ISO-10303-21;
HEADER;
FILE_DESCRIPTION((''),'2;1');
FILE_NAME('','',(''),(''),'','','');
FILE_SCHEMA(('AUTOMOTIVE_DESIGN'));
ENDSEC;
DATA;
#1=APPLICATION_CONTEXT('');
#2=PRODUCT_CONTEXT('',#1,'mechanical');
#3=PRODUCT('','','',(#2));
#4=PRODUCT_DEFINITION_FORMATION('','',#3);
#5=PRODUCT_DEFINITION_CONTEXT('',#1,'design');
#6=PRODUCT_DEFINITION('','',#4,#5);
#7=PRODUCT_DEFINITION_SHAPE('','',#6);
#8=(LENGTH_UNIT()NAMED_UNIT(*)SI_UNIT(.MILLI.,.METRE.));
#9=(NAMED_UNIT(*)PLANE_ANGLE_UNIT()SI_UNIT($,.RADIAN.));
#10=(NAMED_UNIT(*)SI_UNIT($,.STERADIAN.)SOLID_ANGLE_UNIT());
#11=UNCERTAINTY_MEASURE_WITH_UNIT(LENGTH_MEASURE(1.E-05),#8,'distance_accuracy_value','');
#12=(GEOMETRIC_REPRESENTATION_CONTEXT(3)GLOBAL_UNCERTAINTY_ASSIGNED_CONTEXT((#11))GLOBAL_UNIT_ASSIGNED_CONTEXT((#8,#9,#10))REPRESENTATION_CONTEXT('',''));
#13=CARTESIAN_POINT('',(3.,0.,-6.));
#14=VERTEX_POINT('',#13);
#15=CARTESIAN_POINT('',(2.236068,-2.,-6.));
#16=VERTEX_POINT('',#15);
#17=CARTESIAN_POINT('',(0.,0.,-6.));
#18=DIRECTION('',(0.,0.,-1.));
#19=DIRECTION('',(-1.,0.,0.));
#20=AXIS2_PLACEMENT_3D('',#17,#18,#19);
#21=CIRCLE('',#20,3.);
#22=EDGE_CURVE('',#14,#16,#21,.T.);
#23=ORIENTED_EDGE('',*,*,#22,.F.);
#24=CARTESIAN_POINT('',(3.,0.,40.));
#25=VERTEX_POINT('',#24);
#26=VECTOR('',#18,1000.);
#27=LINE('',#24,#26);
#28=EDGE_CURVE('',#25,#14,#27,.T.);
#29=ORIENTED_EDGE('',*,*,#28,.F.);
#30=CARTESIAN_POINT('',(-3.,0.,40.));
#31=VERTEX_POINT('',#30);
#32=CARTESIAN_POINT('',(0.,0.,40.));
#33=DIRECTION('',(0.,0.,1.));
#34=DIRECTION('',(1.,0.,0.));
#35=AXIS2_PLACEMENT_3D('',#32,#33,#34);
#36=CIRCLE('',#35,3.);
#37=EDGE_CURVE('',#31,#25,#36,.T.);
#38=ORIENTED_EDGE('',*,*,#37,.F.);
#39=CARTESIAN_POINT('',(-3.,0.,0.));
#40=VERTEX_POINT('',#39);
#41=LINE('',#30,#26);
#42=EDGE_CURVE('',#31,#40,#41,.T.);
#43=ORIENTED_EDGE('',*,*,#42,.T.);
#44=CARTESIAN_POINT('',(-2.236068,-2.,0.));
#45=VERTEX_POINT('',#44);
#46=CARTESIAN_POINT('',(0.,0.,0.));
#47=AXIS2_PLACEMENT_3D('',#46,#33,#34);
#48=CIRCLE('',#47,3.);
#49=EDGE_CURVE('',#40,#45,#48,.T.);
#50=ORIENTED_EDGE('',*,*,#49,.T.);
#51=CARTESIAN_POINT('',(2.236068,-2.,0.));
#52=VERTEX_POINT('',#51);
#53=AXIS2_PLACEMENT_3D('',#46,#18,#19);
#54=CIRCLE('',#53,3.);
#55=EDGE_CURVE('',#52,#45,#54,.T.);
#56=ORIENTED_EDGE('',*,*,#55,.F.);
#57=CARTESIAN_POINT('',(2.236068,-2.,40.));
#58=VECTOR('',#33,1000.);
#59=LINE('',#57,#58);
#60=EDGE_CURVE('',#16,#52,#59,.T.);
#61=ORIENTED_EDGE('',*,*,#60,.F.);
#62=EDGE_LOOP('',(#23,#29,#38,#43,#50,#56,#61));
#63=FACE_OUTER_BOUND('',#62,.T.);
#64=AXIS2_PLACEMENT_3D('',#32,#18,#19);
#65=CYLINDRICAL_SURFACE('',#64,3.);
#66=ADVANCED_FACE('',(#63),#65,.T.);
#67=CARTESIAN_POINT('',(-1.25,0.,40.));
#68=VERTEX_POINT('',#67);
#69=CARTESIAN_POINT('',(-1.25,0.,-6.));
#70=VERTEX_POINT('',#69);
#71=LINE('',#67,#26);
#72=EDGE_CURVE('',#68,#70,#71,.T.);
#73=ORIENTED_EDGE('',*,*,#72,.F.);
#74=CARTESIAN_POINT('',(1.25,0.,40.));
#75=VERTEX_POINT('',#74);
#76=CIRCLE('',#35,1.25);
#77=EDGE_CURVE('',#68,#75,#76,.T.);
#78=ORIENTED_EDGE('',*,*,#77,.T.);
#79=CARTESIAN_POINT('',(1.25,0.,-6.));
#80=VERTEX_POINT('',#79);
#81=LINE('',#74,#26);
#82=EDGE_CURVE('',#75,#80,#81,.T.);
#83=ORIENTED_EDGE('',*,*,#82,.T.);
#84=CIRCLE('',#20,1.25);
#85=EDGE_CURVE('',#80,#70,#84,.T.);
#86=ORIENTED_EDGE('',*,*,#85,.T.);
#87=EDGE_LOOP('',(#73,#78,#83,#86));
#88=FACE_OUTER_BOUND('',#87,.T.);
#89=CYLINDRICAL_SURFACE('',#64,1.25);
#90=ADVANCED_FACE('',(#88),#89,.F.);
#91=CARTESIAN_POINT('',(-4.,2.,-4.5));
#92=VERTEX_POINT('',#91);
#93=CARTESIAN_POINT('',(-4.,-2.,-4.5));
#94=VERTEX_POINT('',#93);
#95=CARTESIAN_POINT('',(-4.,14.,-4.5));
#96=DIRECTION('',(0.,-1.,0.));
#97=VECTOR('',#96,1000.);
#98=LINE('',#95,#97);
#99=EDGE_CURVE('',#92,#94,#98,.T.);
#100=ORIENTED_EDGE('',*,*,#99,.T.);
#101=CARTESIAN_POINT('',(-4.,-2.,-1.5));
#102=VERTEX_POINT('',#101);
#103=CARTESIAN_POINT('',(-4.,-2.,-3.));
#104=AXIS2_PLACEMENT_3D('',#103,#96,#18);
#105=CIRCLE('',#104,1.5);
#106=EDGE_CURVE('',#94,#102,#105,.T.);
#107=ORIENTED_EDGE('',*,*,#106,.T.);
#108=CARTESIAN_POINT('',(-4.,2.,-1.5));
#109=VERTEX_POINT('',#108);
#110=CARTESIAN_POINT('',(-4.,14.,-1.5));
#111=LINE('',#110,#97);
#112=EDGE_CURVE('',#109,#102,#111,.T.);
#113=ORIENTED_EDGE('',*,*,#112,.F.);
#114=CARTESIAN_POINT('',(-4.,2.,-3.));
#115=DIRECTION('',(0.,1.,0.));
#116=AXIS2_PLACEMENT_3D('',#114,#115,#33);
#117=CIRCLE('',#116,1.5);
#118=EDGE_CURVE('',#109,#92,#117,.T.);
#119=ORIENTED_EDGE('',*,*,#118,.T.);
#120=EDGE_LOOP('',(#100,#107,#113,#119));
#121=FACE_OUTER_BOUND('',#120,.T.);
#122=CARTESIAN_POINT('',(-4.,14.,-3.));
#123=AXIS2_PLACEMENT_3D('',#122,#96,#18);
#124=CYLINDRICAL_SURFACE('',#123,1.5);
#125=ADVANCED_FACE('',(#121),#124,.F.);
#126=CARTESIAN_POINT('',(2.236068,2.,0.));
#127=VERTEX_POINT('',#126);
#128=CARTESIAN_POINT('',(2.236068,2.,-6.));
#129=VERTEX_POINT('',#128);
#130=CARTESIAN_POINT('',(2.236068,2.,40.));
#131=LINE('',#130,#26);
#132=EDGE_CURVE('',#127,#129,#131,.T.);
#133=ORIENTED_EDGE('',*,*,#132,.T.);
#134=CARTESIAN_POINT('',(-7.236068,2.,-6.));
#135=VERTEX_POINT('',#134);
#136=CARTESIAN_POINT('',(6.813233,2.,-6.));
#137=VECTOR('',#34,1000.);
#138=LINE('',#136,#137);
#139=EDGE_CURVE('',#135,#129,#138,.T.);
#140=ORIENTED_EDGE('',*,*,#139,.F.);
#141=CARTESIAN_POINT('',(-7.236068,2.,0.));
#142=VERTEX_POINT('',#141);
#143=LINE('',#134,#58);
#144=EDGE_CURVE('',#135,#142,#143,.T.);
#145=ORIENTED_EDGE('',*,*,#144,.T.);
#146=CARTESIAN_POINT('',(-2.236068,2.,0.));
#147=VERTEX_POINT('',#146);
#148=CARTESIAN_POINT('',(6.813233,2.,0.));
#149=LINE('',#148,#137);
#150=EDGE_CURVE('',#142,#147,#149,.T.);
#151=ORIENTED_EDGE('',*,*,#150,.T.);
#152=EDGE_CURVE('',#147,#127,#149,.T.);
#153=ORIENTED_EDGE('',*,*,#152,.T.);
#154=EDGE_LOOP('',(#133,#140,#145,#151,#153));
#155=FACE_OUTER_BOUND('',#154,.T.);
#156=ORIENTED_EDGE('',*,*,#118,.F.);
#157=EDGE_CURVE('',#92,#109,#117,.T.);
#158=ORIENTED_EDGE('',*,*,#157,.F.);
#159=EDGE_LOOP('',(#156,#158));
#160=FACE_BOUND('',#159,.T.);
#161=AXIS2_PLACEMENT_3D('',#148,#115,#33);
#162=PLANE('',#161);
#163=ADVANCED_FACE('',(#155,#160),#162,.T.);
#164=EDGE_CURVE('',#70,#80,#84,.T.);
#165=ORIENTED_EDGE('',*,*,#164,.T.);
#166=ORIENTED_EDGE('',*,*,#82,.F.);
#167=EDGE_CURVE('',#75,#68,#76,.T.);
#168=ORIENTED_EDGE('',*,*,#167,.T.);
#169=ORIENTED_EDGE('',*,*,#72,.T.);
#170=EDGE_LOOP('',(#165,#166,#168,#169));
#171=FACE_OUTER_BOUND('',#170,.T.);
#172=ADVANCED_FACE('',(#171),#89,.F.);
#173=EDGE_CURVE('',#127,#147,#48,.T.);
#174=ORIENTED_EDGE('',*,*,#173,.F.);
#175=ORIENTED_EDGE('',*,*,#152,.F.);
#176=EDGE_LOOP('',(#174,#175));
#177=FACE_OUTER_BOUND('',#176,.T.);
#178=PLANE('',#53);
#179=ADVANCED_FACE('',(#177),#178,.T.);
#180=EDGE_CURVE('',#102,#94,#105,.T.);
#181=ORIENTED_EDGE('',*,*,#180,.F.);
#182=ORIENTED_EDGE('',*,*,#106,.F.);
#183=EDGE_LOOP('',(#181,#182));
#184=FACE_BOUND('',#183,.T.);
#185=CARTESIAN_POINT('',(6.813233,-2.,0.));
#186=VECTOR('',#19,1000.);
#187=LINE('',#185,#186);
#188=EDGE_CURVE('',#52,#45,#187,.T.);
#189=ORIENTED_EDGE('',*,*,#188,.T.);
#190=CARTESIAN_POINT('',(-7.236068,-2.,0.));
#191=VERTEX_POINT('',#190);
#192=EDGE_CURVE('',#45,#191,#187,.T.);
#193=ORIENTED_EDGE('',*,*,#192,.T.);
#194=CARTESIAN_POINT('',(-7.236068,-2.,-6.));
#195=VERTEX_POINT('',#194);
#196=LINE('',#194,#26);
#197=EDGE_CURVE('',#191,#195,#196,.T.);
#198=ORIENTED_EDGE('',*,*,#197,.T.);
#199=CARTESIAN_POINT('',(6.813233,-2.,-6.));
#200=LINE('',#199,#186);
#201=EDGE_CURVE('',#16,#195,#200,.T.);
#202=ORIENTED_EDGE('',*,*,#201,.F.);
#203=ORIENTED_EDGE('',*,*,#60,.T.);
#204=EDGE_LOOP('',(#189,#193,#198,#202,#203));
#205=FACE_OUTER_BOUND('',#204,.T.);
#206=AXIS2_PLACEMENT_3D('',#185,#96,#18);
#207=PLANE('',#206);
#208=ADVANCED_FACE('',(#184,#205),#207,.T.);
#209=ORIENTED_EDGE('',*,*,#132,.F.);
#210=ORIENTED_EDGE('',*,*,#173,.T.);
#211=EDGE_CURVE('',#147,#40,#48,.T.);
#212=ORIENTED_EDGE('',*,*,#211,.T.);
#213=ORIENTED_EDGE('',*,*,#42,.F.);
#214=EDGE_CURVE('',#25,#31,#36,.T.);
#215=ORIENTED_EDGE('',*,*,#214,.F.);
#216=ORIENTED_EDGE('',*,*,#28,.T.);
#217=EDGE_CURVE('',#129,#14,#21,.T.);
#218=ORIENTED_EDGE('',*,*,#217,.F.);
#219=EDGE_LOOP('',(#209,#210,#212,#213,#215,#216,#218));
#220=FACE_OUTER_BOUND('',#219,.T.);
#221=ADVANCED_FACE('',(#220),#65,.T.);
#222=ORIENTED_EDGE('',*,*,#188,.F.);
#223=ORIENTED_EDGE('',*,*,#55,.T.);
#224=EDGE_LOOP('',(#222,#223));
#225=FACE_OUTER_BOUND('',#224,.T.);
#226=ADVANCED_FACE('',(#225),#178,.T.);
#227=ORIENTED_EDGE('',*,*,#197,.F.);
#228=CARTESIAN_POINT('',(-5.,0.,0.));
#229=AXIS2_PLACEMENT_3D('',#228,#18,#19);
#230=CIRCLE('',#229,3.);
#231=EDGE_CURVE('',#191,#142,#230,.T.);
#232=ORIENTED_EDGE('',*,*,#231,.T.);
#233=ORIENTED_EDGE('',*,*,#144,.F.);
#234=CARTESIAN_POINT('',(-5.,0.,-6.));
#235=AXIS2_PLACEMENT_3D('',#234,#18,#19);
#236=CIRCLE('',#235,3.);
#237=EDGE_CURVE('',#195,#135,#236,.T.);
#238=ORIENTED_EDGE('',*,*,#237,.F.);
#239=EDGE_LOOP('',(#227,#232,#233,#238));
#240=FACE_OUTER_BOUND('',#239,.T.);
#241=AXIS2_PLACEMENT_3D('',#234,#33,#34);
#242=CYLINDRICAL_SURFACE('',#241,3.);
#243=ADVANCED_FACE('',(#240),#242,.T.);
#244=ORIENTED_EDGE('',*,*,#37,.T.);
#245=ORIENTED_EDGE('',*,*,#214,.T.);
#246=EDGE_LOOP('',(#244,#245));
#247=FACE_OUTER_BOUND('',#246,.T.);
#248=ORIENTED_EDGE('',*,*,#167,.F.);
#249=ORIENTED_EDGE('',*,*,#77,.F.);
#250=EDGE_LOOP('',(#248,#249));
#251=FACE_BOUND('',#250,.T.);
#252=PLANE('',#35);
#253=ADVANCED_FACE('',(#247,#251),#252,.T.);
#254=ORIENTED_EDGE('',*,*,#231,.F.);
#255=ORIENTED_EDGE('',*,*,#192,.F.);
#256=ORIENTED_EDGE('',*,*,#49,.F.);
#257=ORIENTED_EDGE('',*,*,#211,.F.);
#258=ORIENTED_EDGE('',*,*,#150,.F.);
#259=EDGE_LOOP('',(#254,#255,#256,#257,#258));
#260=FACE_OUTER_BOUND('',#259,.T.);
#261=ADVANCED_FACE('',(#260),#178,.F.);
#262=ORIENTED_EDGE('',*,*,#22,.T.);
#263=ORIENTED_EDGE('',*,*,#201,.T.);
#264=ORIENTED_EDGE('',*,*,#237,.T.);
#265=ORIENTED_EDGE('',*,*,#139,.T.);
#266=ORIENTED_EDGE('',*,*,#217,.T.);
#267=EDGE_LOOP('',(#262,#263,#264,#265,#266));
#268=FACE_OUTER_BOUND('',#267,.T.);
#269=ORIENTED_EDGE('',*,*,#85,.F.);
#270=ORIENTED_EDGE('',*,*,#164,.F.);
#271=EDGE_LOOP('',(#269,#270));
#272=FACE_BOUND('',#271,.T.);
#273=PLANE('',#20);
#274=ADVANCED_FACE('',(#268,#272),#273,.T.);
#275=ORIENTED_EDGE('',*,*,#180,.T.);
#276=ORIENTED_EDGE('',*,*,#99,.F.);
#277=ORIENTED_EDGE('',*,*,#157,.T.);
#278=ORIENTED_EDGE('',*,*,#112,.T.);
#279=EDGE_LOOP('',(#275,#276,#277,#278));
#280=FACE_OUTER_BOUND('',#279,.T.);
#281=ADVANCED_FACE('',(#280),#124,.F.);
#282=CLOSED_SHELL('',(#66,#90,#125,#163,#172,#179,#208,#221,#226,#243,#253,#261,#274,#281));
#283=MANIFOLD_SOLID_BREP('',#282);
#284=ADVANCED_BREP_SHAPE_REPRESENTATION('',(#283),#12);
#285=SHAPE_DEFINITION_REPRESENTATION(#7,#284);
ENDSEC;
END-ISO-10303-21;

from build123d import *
from build123d.topology import SkipClean

# Parameters (mm, degrees)
SKETCH1_R           = 3
SKETCH1_R_2         = 1.25
BOSS_EXTRUDE1_DEPTH = 40
BOSS_EXTRUDE2_START = 6
SKETCH2_R           = 1.25
BOSS_EXTRUDE2_DEPTH = 6
SKETCH3_W           = 27.527522068
SKETCH3_H           = 18.672368854
SKETCH3_W_2         = 16.126466482
SKETCH3_H_2         = 4
CUT_EXTRUDE1_DEPTH  = 6
SKETCH4_R           = 1.5
CUT_EXTRUDE2_DEPTH  = 16


with BuildPart() as part:
    # Sketch1 → Boss-Extrude1 (new body)
    with BuildSketch(Plane.XY):
        Circle(SKETCH1_R)
        Circle(SKETCH1_R_2, mode=Mode.SUBTRACT)
    extrude(amount=BOSS_EXTRUDE1_DEPTH)

    # Sketch2 → Boss-Extrude2 (add)
    with SkipClean():  # the faces are left unmerged after this step: merging them gives an invalid solid
        with BuildSketch(Plane(origin=(0, 0, 0), x_dir=(-1, 0, 0), z_dir=(0, 0, -1)).offset(BOSS_EXTRUDE2_START)):
            with BuildLine():
                Line((0, 3), (5, 3))
                ThreePointArc((5, 3), (8, 0), (5, -3))
                Line((5, -3), (0, -3))
                ThreePointArc((0, -3), (-3, 0), (0, 3))
            make_face()
            Circle(SKETCH2_R, mode=Mode.SUBTRACT)
        extrude(amount=-BOSS_EXTRUDE2_DEPTH)

    # Sketch3 → Cut-Extrude1 (cut)
    with SkipClean():  # the faces are left unmerged after this step: merging them gives an invalid solid
        with BuildSketch(Plane(origin=(0, 0, -6), x_dir=(-1, 0, 0), z_dir=(0, 0, -1))):
            with Locations((1.25, 0)):
                Rectangle(SKETCH3_W, SKETCH3_H)
            with Locations((1.25, 0)):
                Rectangle(SKETCH3_W_2, SKETCH3_H_2, mode=Mode.SUBTRACT)
        extrude(amount=-CUT_EXTRUDE1_DEPTH, mode=Mode.SUBTRACT)

    # Sketch4 → Cut-Extrude2 (cut)
    with SkipClean():  # the faces are left unmerged after this step: merging them gives an invalid solid
        with BuildSketch(Plane(origin=(0, -2, 0), x_dir=(-1, 0, 0), z_dir=(0, -1, 0))):
            with Locations(Location((4, 3, 0), (0, 0, 90))):
                Circle(SKETCH4_R)
        extrude(amount=-CUT_EXTRUDE2_DEPTH, mode=Mode.SUBTRACT)


solid = part.part
